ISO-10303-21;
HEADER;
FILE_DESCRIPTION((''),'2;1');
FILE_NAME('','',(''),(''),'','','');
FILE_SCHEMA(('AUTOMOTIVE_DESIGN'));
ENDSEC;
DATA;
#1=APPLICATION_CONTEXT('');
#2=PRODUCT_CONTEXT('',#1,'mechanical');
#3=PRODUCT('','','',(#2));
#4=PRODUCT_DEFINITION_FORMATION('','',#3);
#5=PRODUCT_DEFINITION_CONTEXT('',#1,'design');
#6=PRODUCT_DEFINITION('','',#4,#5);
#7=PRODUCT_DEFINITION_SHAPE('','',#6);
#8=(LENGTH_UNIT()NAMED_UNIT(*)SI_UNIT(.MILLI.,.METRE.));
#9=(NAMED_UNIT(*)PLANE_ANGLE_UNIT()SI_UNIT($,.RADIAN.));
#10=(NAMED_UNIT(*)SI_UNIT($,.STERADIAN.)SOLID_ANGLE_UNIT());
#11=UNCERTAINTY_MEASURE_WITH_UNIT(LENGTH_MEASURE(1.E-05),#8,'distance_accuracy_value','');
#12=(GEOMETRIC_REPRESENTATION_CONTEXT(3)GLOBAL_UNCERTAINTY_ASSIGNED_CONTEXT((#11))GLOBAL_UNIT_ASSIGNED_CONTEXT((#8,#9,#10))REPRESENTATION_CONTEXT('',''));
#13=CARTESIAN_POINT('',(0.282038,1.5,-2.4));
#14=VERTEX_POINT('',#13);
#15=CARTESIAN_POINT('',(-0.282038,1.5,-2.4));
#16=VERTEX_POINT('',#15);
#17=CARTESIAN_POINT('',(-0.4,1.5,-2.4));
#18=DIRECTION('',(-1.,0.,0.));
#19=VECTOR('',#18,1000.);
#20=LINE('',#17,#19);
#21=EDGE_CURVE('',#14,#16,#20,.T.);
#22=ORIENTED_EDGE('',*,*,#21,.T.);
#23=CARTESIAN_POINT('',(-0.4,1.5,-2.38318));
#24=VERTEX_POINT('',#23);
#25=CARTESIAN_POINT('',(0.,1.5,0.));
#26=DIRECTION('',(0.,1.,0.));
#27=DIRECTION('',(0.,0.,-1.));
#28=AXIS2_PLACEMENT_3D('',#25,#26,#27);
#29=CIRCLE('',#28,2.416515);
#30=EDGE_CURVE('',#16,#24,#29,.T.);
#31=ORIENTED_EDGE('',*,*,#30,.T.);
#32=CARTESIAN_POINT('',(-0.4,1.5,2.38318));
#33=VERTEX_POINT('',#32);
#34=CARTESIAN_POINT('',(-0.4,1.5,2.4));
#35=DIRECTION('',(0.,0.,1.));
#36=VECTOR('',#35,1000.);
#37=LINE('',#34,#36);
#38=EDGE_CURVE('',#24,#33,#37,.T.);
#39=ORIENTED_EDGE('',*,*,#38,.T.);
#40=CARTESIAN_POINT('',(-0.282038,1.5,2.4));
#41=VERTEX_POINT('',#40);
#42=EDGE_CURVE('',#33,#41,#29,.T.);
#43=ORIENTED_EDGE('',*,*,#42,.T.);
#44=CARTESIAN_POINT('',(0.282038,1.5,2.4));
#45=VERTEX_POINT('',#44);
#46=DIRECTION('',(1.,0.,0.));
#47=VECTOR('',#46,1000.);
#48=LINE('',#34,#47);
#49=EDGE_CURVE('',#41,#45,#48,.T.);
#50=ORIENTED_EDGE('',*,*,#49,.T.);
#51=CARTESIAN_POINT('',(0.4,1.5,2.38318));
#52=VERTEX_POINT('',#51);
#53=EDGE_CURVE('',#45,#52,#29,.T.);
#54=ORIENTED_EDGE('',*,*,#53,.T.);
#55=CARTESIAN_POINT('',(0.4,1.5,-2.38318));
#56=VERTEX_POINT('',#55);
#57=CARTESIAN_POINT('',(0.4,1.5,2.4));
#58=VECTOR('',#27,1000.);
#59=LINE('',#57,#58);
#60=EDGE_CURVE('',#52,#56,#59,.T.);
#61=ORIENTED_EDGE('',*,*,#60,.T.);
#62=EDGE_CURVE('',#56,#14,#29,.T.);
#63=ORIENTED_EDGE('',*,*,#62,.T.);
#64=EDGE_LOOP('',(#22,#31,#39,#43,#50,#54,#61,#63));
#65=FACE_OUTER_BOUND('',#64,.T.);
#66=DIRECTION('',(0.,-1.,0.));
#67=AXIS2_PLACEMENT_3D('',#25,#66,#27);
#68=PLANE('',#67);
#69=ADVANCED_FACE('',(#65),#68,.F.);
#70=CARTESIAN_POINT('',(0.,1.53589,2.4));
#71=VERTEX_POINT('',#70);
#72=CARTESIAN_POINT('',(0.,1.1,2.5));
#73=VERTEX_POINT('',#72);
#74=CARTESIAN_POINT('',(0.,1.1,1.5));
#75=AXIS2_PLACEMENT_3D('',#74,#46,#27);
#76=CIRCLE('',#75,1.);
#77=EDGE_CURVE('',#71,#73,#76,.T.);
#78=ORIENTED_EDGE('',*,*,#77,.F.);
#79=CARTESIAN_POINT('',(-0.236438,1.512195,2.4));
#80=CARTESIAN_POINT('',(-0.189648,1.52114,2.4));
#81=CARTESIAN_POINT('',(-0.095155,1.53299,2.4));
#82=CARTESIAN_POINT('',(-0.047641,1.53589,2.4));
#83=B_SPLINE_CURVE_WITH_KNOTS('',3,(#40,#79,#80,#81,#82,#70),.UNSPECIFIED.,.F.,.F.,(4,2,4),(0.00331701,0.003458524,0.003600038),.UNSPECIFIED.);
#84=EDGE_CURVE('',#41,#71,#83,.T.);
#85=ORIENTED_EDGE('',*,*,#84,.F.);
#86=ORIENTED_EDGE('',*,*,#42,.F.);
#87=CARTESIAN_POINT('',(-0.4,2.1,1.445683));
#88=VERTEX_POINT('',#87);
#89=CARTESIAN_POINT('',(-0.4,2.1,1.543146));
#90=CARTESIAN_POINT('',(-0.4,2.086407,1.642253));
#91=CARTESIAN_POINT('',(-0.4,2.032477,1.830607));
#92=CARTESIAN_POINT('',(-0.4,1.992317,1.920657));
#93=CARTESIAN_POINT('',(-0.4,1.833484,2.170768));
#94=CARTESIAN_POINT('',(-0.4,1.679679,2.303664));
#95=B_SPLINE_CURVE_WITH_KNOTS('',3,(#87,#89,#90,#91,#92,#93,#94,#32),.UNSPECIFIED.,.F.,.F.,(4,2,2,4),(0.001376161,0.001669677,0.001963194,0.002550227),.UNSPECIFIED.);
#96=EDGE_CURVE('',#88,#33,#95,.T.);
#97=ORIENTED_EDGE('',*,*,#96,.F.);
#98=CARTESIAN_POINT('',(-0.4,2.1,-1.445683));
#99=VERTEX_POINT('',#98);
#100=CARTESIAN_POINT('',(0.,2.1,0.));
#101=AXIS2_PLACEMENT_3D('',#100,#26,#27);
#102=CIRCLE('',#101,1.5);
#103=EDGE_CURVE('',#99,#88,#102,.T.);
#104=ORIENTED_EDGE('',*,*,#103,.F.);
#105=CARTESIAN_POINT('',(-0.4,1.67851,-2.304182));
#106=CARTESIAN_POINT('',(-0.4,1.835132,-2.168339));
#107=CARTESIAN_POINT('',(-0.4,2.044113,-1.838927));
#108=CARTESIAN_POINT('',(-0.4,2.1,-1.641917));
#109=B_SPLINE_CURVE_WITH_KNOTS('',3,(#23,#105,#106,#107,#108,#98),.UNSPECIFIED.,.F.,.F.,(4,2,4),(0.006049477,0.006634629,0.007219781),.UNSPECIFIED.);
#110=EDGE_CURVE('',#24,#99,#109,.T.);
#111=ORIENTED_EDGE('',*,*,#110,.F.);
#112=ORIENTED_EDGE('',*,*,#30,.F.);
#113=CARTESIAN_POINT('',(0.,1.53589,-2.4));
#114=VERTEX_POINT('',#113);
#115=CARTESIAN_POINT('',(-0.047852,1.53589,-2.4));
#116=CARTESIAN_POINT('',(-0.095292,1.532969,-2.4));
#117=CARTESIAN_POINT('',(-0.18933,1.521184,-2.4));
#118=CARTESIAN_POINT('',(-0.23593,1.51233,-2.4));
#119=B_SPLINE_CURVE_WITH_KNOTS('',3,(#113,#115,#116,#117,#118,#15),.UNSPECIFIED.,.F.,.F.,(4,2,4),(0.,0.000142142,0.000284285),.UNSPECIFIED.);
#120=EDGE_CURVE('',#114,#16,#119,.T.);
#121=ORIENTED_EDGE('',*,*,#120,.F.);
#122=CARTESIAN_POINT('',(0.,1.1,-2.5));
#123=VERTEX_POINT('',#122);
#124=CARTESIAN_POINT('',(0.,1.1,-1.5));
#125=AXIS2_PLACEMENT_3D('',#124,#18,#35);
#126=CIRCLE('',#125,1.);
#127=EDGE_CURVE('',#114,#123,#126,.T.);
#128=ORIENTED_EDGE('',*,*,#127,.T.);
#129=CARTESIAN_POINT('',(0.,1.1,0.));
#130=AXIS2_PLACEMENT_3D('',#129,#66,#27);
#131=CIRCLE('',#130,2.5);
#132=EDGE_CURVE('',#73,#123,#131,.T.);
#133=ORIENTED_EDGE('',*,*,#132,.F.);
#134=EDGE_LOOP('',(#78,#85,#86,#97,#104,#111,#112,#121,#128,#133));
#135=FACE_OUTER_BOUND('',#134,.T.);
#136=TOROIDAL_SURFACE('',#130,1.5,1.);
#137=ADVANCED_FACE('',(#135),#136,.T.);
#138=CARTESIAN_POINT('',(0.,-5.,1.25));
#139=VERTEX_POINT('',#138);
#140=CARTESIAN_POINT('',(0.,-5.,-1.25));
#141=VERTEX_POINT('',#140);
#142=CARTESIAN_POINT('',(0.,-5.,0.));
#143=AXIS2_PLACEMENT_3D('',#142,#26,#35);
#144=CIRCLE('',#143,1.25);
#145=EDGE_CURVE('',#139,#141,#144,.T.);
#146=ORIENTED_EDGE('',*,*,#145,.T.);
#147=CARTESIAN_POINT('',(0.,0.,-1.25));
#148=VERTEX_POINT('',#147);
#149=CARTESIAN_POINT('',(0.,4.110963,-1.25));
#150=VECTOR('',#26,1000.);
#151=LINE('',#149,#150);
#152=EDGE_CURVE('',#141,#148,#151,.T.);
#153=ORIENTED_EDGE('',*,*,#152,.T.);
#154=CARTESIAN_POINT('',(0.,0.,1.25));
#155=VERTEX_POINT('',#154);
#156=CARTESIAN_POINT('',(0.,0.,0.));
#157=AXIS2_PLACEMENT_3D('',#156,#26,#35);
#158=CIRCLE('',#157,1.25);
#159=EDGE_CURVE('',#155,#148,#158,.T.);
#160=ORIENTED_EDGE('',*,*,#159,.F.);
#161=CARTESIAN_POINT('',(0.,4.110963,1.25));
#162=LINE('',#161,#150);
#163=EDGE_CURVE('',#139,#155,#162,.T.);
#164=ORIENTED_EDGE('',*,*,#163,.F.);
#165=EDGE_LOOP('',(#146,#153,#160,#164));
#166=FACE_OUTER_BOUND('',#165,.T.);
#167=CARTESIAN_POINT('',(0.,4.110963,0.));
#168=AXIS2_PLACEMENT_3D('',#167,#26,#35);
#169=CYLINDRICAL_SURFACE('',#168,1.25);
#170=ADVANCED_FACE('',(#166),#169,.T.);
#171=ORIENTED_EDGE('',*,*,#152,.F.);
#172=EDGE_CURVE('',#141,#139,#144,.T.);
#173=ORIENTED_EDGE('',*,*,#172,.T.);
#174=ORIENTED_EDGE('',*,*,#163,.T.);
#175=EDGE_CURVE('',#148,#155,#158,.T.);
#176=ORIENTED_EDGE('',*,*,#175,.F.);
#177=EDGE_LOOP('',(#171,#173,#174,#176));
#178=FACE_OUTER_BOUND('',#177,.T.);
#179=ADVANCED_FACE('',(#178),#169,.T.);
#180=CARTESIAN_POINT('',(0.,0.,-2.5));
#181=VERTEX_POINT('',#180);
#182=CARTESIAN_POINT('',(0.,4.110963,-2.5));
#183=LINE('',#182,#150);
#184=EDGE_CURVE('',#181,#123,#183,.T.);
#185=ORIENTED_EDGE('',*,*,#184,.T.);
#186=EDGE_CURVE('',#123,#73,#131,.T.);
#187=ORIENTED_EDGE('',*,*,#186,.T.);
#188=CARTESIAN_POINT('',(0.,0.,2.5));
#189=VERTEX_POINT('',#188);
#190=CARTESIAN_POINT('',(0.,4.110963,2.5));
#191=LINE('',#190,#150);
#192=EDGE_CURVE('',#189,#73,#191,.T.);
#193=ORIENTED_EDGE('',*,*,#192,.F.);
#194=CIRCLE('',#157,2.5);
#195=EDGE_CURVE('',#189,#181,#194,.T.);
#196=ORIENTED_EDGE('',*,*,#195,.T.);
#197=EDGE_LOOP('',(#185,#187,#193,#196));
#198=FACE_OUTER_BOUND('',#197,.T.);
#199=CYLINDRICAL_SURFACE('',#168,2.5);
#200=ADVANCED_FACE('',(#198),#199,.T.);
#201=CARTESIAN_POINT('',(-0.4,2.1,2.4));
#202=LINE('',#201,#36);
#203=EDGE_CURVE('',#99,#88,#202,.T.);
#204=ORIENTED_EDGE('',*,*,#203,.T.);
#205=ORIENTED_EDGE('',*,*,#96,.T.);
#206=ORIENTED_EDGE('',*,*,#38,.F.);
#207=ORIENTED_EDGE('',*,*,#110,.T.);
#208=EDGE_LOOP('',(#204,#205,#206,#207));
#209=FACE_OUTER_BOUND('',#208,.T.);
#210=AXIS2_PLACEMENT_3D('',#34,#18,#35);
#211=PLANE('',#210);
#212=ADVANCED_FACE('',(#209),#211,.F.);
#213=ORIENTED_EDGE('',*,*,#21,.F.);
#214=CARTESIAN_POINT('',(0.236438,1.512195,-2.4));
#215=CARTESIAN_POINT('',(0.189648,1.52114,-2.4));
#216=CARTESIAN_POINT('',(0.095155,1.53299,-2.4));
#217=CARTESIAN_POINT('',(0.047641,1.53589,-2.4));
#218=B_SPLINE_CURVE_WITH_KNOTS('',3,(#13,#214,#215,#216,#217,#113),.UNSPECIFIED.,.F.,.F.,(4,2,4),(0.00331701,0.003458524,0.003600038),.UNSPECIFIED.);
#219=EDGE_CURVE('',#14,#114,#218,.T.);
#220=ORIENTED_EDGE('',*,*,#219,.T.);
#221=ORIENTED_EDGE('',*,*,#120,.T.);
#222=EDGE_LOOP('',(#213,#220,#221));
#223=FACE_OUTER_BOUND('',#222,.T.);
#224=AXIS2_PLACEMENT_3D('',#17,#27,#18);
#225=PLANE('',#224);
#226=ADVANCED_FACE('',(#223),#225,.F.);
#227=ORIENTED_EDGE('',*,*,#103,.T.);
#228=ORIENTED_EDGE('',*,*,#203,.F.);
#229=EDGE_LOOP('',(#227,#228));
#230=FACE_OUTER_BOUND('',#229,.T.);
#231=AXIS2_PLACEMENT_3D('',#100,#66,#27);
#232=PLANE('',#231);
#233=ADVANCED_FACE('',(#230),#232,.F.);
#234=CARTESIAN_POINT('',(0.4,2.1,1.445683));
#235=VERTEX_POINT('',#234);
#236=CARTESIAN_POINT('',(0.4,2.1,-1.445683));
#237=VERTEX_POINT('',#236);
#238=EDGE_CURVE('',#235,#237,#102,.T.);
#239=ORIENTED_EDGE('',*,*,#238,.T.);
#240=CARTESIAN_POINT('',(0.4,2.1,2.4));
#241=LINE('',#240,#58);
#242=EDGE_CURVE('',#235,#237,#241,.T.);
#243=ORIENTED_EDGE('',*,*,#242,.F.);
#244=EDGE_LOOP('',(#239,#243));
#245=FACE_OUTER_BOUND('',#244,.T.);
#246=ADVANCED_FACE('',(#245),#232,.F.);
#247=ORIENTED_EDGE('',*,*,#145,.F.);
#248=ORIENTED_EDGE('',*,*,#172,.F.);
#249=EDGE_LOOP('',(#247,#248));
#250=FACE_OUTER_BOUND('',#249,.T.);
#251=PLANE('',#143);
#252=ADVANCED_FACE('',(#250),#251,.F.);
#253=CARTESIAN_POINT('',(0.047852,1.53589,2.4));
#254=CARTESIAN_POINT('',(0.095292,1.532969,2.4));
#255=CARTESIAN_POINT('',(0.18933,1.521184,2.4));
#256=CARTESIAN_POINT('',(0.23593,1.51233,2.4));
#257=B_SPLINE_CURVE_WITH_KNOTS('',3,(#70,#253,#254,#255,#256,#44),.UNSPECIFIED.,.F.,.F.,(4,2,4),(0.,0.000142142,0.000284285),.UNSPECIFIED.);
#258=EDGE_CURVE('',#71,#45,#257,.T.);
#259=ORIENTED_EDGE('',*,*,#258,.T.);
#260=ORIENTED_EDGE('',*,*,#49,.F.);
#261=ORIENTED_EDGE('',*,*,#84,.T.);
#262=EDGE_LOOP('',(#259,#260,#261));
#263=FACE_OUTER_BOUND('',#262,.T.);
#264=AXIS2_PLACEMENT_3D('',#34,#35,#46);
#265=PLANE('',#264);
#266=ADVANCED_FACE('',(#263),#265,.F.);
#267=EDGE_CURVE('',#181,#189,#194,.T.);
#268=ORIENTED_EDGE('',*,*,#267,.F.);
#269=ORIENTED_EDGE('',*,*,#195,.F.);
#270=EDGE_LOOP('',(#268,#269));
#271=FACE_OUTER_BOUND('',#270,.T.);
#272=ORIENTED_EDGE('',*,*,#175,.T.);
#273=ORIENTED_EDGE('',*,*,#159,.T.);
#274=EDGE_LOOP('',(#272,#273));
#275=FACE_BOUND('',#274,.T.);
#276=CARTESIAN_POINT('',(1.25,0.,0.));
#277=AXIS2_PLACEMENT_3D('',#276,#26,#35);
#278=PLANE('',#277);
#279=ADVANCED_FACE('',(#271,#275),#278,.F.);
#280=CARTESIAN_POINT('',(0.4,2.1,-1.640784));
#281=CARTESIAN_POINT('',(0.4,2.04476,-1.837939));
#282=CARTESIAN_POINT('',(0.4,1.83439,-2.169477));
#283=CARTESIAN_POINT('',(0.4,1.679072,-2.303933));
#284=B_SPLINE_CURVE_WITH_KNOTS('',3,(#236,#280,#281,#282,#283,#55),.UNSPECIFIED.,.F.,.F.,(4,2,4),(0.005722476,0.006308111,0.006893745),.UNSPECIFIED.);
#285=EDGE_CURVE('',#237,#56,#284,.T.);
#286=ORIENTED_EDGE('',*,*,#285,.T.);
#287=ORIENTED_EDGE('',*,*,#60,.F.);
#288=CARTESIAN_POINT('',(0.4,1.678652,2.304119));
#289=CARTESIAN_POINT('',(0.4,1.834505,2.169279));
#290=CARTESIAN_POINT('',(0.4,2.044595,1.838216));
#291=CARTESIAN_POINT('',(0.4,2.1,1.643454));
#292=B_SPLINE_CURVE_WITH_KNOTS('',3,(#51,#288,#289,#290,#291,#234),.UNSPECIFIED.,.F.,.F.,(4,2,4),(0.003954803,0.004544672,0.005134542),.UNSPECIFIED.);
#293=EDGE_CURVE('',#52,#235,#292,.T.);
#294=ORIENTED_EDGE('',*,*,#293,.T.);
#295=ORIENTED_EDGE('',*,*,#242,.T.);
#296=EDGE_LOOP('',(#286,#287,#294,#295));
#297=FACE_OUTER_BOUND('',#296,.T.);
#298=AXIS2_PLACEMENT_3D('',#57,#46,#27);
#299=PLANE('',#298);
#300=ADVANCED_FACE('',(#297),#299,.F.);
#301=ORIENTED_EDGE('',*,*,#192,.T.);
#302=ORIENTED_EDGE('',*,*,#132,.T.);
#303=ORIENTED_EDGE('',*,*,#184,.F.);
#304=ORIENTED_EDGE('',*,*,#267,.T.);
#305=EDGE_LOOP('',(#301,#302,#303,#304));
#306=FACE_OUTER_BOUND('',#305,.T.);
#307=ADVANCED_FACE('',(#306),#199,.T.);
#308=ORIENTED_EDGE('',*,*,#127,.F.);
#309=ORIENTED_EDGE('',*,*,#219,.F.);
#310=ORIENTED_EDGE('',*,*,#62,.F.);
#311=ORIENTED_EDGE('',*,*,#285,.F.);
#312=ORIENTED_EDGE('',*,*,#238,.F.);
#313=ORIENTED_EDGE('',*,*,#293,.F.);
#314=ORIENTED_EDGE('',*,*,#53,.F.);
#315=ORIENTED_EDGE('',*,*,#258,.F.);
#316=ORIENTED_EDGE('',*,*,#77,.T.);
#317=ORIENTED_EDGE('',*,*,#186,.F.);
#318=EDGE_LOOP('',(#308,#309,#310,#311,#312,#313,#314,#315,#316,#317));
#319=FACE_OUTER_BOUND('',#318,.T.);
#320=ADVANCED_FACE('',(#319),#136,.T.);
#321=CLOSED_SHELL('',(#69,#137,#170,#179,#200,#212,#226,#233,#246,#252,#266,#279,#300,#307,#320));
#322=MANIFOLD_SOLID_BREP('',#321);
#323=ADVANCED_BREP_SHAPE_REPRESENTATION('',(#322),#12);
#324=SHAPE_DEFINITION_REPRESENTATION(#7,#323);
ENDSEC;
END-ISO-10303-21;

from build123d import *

# Parameters (mm, degrees)
HEAD_EDGE_FILLET_R1_R            = 1
SCREWDRIVER_SLOT_SKETCH_W        = 0.8
SCREWDRIVER_SLOT_SKETCH_H        = 4.8
SCREWDRIVER_SLOT_0_8_X_0_6_DEPTH = 0.6


with BuildPart() as part:
    # Bolt Profile Sketch → Bolt Body Ø2.5 Shank Ø5 Head (revolve)
    with BuildSketch(Plane.XY, mode=Mode.PRIVATE) as bolt_body_2_5_shank_5_head_sk:
        Polygon((0, -5), (1.25, -5), (1.25, 0), (2.5, 0), (2.5, 2.1), (0, 2.1), align=None)
    revolve(bolt_body_2_5_shank_5_head_sk.sketch.rotate(Axis((0, 4.110962567, 0), (0, -1, 0)), 90), axis=Axis((0, 4.110962567, 0), (0, -1, 0)))

    # Head Edge Fillet R1
    head_edge_fillet_r1_edges = [part.edges().sort_by_distance(p)[0] for p in [
        (0, 2.1, -2.5),
    ]]
    fillet(head_edge_fillet_r1_edges, radius=HEAD_EDGE_FILLET_R1_R)

    # Screwdriver Slot Sketch → Screwdriver Slot 0.8 x 0.6 (cut)
    with BuildSketch(Plane(origin=(0, 2.1, 0), x_dir=(1, 0, 0), z_dir=(0, 1, 0))):
        Rectangle(SCREWDRIVER_SLOT_SKETCH_W, SCREWDRIVER_SLOT_SKETCH_H)
    extrude(amount=-SCREWDRIVER_SLOT_0_8_X_0_6_DEPTH, mode=Mode.SUBTRACT)


solid = part.part
